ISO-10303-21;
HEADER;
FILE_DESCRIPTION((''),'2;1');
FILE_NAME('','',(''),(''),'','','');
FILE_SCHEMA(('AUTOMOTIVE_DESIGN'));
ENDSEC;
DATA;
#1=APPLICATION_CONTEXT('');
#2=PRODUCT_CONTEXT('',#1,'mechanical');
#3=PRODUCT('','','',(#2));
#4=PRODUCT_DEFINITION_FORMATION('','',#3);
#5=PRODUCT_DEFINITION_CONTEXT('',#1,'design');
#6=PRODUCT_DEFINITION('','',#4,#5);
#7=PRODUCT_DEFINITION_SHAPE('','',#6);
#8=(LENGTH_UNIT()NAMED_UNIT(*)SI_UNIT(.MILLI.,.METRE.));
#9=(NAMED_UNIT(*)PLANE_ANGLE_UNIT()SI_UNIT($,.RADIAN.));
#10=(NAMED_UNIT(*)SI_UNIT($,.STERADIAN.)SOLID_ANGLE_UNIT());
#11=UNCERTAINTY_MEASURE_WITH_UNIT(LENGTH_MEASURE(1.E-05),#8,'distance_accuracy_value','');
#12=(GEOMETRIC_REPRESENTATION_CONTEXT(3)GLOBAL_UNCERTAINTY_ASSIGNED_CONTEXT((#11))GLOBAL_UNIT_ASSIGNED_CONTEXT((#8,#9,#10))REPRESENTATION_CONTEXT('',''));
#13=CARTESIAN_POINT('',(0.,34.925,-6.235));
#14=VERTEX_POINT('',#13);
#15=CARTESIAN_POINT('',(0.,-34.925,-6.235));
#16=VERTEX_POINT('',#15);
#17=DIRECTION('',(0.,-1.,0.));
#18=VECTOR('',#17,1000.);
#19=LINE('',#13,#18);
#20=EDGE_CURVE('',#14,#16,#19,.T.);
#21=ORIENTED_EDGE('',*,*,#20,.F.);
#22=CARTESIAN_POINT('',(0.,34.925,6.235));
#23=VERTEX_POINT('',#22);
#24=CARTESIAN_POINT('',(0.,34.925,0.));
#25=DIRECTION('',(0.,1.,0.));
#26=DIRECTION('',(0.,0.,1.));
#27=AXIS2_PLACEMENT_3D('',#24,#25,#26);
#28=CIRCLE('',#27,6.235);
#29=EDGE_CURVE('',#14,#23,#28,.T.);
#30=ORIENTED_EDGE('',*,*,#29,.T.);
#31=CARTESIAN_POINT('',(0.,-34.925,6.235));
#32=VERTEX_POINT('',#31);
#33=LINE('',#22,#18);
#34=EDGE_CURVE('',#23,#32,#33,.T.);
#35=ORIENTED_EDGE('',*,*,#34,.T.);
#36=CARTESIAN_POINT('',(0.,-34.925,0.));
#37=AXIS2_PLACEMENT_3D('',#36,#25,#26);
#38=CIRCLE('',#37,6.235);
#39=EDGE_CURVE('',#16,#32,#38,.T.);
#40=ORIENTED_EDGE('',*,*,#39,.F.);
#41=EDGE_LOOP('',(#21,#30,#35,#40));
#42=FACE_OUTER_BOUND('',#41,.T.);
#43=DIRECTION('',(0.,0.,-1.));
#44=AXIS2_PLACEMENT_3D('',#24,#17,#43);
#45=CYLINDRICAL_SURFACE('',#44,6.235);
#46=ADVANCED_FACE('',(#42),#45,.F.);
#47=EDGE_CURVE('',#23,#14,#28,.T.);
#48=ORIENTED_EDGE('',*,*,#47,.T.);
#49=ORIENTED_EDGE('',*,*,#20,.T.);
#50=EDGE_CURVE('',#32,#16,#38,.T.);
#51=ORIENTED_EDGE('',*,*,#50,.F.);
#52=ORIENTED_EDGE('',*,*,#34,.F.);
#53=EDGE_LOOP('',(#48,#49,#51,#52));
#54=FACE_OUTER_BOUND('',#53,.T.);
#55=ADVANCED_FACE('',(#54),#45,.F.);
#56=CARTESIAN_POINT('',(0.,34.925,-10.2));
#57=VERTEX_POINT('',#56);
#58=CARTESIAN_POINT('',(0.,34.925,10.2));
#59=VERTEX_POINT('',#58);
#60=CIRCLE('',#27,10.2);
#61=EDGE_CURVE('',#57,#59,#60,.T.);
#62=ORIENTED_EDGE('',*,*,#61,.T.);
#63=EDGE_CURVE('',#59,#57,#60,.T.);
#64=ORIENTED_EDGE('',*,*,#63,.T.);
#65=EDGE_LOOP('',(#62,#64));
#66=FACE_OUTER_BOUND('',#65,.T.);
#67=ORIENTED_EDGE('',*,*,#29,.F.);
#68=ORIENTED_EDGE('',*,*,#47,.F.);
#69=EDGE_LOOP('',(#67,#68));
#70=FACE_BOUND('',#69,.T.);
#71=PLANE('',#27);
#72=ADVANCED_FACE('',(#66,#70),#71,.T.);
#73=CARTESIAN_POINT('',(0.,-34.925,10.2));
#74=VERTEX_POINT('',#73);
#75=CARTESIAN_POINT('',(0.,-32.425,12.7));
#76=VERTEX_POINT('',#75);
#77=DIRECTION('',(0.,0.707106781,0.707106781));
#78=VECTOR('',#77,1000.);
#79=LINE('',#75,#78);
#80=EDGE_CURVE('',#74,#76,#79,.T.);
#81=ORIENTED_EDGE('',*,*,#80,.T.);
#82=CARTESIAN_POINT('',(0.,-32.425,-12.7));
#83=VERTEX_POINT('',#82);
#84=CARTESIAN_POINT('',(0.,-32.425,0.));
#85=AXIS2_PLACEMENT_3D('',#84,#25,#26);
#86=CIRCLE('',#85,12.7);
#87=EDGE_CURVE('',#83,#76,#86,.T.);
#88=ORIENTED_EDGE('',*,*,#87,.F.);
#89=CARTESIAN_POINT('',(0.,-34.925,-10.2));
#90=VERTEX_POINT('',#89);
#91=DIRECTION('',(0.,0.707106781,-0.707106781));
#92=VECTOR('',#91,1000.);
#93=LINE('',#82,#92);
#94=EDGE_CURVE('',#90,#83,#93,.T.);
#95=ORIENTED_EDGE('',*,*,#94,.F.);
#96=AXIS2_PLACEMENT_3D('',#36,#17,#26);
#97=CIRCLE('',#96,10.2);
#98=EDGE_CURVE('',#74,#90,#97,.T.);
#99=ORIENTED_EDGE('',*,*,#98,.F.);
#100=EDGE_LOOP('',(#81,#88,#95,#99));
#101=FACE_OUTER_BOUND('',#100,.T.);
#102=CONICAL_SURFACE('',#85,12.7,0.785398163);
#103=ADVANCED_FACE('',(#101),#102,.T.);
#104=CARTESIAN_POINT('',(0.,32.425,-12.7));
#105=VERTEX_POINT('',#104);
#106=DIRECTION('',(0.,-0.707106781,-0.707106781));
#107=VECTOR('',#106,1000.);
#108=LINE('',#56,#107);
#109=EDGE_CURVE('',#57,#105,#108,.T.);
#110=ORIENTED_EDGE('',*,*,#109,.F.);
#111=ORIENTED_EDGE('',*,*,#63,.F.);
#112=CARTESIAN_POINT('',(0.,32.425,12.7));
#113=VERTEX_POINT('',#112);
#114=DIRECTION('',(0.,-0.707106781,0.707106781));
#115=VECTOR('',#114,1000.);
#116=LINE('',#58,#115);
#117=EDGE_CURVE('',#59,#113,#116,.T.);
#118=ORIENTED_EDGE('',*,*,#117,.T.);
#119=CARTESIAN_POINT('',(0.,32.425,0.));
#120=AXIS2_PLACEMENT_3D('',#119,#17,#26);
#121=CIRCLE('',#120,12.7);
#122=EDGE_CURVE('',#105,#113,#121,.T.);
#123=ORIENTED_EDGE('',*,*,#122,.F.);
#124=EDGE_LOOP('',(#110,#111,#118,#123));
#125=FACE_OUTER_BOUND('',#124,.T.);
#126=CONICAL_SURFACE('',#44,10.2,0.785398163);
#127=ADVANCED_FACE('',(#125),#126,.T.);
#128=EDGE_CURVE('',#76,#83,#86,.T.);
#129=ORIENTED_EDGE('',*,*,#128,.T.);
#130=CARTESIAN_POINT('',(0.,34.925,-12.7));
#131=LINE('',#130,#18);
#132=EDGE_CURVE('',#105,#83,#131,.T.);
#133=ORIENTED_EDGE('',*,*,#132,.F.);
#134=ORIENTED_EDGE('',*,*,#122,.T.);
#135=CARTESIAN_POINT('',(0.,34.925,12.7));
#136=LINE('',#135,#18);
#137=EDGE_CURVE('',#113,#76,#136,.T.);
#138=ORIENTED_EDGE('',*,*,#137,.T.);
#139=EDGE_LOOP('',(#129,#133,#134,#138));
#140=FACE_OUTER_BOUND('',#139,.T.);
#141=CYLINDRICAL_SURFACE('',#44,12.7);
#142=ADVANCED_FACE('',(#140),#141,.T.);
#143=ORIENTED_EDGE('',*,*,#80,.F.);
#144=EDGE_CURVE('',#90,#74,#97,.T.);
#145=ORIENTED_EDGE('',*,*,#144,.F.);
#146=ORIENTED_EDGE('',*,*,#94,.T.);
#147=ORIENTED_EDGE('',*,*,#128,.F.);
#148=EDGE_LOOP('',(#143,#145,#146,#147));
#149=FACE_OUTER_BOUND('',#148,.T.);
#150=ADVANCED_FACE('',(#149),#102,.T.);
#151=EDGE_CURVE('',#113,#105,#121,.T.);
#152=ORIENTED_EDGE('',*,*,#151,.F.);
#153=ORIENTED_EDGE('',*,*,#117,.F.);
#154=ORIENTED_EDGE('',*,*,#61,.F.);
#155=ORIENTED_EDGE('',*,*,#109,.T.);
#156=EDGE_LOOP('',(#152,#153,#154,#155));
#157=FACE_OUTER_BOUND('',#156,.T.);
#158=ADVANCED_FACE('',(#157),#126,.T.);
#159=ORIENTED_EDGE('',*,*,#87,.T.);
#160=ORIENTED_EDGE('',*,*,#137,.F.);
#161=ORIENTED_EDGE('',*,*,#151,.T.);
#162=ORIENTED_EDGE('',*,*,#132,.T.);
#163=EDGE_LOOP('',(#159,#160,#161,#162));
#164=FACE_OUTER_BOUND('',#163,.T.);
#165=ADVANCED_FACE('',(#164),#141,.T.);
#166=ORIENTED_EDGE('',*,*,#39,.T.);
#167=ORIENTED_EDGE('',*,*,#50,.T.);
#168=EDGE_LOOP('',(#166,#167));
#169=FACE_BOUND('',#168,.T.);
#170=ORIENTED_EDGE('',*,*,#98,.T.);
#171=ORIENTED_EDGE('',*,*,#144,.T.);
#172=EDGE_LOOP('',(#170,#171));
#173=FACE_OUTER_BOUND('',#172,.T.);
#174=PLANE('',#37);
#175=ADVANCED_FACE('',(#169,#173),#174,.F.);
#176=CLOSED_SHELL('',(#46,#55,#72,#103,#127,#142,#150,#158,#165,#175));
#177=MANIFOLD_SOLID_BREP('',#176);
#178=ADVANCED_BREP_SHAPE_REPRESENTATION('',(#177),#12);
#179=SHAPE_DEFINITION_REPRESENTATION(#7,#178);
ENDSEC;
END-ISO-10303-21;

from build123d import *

# Parameters (mm, degrees)
PIN_PROFILE_25_4_12_47_R   = 12.7
PIN_PROFILE_25_4_12_47_R_2 = 6.235
PIN_BODY_69_85_DEPTH       = 34.925
END_CHAMFERS_2_5X45_SIZE   = 2.5


with BuildPart() as part:
    # Pin Profile Ø25.4-Ø12.47 → Pin Body 69.85 (new, symmetric)
    with BuildSketch(Plane(origin=(0, 0, 0), x_dir=(1, 0, 0), z_dir=(0, 1, 0))):
        with Locations(Location((0, 0, 0), (0, 0, 270))):
            Circle(PIN_PROFILE_25_4_12_47_R)
        with Locations(Location((0, 0, 0), (0, 0, 270))):
            Circle(PIN_PROFILE_25_4_12_47_R_2, mode=Mode.SUBTRACT)
    extrude(amount=PIN_BODY_69_85_DEPTH, both=True)

    # End Chamfers 2.5x45°
    end_chamfers_2_5x45_edges = [part.edges().sort_by_distance(p)[0] for p in [
        (0, -34.925, -12.7),
        (0, 34.925, -12.7),
    ]]
    chamfer(end_chamfers_2_5x45_edges, length=END_CHAMFERS_2_5X45_SIZE)


solid = part.part
